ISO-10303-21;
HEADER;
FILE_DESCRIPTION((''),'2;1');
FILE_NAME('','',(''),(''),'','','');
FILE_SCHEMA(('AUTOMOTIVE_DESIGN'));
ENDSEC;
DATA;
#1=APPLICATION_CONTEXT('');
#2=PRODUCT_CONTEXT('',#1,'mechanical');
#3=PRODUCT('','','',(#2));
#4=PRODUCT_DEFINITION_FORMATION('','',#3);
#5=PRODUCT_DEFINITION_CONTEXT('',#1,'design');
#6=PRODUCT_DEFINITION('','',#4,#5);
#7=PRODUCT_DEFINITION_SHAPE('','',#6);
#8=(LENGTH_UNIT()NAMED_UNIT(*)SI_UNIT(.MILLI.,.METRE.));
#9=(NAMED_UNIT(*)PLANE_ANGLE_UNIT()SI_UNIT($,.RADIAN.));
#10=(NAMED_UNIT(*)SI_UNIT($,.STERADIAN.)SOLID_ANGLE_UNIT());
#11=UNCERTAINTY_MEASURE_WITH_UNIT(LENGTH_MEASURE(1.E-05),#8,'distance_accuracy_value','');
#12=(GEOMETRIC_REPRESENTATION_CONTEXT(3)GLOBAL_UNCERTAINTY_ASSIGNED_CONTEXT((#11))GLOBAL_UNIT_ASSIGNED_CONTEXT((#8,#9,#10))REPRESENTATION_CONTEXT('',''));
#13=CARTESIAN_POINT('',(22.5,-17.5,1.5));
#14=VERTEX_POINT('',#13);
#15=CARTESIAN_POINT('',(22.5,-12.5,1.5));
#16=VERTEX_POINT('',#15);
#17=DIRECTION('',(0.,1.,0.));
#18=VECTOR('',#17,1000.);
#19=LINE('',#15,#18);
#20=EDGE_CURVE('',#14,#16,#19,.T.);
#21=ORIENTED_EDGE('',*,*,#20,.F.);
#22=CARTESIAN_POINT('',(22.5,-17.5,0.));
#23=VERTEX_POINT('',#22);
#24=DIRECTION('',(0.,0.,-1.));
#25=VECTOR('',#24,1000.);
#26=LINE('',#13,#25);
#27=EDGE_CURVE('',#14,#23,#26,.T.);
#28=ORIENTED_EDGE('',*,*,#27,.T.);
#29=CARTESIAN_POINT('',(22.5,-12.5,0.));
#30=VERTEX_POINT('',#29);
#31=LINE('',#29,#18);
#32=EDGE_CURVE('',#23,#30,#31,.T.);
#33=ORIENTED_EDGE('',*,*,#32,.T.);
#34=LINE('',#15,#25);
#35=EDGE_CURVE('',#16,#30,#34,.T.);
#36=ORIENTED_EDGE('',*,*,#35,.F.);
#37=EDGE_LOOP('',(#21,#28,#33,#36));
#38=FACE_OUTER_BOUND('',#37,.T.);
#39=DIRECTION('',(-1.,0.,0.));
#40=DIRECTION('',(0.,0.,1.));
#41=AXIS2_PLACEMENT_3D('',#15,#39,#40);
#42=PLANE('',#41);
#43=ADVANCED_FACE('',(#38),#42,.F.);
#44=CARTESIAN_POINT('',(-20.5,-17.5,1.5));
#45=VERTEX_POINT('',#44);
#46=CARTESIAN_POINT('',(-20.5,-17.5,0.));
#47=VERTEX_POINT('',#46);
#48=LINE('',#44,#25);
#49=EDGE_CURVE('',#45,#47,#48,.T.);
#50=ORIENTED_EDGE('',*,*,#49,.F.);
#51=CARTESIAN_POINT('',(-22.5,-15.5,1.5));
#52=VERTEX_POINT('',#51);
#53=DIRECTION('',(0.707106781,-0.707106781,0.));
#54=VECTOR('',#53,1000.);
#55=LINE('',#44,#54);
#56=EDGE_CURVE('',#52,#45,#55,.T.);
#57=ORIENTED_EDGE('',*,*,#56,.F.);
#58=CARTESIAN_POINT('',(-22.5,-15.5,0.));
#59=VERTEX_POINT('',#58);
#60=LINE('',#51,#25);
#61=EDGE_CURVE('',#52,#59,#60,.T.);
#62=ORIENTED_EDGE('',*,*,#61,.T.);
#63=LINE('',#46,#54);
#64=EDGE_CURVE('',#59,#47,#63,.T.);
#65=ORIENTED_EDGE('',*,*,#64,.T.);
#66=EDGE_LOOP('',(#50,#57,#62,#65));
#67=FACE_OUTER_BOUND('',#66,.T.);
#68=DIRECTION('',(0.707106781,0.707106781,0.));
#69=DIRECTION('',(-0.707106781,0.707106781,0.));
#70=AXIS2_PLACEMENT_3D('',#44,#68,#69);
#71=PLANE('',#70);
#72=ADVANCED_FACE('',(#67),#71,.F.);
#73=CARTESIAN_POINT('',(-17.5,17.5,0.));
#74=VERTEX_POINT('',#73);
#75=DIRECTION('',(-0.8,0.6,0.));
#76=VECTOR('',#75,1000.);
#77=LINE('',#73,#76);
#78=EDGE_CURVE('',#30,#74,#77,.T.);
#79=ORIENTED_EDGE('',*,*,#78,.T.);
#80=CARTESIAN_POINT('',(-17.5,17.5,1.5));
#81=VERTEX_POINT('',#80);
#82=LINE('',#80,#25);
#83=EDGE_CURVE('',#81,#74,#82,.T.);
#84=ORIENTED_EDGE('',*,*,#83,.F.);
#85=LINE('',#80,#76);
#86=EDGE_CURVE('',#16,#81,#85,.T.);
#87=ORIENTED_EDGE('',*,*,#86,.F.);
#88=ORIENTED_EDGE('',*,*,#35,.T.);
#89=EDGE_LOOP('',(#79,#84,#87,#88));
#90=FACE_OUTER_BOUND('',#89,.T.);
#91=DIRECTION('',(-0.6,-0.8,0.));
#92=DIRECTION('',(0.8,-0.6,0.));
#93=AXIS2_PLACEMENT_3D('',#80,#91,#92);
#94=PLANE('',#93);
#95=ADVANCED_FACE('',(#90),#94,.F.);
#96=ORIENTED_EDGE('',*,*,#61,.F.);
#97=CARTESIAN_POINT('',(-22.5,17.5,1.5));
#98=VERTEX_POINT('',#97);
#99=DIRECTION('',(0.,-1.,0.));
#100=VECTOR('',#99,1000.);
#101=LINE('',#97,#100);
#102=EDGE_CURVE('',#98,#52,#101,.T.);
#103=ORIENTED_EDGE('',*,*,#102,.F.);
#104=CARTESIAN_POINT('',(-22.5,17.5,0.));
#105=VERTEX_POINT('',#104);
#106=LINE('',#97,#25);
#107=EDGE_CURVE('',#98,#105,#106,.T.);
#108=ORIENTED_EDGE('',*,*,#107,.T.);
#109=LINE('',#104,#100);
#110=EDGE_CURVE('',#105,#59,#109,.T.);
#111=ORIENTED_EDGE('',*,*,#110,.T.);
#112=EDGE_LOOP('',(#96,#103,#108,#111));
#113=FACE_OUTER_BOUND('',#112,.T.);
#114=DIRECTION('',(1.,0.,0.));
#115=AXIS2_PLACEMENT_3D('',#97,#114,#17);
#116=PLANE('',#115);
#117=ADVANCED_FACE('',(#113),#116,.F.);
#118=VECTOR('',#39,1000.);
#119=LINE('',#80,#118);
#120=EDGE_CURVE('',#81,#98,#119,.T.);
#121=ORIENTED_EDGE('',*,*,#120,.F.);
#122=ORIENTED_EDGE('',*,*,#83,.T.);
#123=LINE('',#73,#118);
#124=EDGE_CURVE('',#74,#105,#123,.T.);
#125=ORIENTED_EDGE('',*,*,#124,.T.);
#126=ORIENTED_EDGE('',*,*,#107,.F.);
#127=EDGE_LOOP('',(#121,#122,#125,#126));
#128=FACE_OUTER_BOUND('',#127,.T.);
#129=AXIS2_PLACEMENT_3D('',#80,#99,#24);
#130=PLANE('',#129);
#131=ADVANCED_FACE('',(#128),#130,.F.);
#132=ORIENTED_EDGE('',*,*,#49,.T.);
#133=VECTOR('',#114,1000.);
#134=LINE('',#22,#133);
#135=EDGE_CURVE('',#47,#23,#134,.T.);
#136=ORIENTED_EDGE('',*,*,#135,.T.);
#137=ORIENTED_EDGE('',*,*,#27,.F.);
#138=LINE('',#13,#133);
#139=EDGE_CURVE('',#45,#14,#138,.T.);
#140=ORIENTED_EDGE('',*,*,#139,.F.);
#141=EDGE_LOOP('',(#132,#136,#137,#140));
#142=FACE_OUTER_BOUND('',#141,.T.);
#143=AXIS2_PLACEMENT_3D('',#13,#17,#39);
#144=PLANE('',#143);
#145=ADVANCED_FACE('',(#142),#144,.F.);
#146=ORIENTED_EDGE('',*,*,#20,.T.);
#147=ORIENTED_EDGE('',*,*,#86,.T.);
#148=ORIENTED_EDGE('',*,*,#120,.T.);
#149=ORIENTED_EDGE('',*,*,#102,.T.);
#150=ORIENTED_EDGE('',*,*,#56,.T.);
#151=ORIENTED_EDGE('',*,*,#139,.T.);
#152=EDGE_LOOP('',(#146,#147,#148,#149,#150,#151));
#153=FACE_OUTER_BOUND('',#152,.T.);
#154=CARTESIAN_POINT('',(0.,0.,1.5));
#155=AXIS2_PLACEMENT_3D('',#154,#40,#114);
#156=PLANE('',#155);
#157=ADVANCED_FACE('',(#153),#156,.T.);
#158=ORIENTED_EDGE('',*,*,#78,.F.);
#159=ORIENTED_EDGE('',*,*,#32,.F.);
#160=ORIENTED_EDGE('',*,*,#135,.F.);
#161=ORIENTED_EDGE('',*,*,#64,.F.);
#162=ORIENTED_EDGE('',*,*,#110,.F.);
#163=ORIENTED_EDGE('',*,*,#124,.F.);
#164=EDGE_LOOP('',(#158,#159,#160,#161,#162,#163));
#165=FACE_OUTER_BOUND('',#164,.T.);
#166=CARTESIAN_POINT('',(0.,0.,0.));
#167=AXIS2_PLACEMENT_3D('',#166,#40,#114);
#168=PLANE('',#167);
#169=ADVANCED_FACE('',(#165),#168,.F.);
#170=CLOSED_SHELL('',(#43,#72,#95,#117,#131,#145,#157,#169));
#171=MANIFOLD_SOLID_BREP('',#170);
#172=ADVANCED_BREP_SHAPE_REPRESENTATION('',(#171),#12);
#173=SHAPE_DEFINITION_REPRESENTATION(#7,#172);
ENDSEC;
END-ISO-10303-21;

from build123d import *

# Parameters (mm, degrees)
BOSS_EXTRUDE1_DEPTH = 1.5


with BuildPart() as part:
    # Sketch1 → Boss-Extrude1 (new body)
    with BuildSketch(Plane.XY):
        Polygon((-17.5, 17.5), (22.5, -12.5), (22.5, -17.5), (-20.5, -17.5), (-22.5, -15.5), (-22.5, 17.5), align=None)
    extrude(amount=BOSS_EXTRUDE1_DEPTH)


solid = part.part
